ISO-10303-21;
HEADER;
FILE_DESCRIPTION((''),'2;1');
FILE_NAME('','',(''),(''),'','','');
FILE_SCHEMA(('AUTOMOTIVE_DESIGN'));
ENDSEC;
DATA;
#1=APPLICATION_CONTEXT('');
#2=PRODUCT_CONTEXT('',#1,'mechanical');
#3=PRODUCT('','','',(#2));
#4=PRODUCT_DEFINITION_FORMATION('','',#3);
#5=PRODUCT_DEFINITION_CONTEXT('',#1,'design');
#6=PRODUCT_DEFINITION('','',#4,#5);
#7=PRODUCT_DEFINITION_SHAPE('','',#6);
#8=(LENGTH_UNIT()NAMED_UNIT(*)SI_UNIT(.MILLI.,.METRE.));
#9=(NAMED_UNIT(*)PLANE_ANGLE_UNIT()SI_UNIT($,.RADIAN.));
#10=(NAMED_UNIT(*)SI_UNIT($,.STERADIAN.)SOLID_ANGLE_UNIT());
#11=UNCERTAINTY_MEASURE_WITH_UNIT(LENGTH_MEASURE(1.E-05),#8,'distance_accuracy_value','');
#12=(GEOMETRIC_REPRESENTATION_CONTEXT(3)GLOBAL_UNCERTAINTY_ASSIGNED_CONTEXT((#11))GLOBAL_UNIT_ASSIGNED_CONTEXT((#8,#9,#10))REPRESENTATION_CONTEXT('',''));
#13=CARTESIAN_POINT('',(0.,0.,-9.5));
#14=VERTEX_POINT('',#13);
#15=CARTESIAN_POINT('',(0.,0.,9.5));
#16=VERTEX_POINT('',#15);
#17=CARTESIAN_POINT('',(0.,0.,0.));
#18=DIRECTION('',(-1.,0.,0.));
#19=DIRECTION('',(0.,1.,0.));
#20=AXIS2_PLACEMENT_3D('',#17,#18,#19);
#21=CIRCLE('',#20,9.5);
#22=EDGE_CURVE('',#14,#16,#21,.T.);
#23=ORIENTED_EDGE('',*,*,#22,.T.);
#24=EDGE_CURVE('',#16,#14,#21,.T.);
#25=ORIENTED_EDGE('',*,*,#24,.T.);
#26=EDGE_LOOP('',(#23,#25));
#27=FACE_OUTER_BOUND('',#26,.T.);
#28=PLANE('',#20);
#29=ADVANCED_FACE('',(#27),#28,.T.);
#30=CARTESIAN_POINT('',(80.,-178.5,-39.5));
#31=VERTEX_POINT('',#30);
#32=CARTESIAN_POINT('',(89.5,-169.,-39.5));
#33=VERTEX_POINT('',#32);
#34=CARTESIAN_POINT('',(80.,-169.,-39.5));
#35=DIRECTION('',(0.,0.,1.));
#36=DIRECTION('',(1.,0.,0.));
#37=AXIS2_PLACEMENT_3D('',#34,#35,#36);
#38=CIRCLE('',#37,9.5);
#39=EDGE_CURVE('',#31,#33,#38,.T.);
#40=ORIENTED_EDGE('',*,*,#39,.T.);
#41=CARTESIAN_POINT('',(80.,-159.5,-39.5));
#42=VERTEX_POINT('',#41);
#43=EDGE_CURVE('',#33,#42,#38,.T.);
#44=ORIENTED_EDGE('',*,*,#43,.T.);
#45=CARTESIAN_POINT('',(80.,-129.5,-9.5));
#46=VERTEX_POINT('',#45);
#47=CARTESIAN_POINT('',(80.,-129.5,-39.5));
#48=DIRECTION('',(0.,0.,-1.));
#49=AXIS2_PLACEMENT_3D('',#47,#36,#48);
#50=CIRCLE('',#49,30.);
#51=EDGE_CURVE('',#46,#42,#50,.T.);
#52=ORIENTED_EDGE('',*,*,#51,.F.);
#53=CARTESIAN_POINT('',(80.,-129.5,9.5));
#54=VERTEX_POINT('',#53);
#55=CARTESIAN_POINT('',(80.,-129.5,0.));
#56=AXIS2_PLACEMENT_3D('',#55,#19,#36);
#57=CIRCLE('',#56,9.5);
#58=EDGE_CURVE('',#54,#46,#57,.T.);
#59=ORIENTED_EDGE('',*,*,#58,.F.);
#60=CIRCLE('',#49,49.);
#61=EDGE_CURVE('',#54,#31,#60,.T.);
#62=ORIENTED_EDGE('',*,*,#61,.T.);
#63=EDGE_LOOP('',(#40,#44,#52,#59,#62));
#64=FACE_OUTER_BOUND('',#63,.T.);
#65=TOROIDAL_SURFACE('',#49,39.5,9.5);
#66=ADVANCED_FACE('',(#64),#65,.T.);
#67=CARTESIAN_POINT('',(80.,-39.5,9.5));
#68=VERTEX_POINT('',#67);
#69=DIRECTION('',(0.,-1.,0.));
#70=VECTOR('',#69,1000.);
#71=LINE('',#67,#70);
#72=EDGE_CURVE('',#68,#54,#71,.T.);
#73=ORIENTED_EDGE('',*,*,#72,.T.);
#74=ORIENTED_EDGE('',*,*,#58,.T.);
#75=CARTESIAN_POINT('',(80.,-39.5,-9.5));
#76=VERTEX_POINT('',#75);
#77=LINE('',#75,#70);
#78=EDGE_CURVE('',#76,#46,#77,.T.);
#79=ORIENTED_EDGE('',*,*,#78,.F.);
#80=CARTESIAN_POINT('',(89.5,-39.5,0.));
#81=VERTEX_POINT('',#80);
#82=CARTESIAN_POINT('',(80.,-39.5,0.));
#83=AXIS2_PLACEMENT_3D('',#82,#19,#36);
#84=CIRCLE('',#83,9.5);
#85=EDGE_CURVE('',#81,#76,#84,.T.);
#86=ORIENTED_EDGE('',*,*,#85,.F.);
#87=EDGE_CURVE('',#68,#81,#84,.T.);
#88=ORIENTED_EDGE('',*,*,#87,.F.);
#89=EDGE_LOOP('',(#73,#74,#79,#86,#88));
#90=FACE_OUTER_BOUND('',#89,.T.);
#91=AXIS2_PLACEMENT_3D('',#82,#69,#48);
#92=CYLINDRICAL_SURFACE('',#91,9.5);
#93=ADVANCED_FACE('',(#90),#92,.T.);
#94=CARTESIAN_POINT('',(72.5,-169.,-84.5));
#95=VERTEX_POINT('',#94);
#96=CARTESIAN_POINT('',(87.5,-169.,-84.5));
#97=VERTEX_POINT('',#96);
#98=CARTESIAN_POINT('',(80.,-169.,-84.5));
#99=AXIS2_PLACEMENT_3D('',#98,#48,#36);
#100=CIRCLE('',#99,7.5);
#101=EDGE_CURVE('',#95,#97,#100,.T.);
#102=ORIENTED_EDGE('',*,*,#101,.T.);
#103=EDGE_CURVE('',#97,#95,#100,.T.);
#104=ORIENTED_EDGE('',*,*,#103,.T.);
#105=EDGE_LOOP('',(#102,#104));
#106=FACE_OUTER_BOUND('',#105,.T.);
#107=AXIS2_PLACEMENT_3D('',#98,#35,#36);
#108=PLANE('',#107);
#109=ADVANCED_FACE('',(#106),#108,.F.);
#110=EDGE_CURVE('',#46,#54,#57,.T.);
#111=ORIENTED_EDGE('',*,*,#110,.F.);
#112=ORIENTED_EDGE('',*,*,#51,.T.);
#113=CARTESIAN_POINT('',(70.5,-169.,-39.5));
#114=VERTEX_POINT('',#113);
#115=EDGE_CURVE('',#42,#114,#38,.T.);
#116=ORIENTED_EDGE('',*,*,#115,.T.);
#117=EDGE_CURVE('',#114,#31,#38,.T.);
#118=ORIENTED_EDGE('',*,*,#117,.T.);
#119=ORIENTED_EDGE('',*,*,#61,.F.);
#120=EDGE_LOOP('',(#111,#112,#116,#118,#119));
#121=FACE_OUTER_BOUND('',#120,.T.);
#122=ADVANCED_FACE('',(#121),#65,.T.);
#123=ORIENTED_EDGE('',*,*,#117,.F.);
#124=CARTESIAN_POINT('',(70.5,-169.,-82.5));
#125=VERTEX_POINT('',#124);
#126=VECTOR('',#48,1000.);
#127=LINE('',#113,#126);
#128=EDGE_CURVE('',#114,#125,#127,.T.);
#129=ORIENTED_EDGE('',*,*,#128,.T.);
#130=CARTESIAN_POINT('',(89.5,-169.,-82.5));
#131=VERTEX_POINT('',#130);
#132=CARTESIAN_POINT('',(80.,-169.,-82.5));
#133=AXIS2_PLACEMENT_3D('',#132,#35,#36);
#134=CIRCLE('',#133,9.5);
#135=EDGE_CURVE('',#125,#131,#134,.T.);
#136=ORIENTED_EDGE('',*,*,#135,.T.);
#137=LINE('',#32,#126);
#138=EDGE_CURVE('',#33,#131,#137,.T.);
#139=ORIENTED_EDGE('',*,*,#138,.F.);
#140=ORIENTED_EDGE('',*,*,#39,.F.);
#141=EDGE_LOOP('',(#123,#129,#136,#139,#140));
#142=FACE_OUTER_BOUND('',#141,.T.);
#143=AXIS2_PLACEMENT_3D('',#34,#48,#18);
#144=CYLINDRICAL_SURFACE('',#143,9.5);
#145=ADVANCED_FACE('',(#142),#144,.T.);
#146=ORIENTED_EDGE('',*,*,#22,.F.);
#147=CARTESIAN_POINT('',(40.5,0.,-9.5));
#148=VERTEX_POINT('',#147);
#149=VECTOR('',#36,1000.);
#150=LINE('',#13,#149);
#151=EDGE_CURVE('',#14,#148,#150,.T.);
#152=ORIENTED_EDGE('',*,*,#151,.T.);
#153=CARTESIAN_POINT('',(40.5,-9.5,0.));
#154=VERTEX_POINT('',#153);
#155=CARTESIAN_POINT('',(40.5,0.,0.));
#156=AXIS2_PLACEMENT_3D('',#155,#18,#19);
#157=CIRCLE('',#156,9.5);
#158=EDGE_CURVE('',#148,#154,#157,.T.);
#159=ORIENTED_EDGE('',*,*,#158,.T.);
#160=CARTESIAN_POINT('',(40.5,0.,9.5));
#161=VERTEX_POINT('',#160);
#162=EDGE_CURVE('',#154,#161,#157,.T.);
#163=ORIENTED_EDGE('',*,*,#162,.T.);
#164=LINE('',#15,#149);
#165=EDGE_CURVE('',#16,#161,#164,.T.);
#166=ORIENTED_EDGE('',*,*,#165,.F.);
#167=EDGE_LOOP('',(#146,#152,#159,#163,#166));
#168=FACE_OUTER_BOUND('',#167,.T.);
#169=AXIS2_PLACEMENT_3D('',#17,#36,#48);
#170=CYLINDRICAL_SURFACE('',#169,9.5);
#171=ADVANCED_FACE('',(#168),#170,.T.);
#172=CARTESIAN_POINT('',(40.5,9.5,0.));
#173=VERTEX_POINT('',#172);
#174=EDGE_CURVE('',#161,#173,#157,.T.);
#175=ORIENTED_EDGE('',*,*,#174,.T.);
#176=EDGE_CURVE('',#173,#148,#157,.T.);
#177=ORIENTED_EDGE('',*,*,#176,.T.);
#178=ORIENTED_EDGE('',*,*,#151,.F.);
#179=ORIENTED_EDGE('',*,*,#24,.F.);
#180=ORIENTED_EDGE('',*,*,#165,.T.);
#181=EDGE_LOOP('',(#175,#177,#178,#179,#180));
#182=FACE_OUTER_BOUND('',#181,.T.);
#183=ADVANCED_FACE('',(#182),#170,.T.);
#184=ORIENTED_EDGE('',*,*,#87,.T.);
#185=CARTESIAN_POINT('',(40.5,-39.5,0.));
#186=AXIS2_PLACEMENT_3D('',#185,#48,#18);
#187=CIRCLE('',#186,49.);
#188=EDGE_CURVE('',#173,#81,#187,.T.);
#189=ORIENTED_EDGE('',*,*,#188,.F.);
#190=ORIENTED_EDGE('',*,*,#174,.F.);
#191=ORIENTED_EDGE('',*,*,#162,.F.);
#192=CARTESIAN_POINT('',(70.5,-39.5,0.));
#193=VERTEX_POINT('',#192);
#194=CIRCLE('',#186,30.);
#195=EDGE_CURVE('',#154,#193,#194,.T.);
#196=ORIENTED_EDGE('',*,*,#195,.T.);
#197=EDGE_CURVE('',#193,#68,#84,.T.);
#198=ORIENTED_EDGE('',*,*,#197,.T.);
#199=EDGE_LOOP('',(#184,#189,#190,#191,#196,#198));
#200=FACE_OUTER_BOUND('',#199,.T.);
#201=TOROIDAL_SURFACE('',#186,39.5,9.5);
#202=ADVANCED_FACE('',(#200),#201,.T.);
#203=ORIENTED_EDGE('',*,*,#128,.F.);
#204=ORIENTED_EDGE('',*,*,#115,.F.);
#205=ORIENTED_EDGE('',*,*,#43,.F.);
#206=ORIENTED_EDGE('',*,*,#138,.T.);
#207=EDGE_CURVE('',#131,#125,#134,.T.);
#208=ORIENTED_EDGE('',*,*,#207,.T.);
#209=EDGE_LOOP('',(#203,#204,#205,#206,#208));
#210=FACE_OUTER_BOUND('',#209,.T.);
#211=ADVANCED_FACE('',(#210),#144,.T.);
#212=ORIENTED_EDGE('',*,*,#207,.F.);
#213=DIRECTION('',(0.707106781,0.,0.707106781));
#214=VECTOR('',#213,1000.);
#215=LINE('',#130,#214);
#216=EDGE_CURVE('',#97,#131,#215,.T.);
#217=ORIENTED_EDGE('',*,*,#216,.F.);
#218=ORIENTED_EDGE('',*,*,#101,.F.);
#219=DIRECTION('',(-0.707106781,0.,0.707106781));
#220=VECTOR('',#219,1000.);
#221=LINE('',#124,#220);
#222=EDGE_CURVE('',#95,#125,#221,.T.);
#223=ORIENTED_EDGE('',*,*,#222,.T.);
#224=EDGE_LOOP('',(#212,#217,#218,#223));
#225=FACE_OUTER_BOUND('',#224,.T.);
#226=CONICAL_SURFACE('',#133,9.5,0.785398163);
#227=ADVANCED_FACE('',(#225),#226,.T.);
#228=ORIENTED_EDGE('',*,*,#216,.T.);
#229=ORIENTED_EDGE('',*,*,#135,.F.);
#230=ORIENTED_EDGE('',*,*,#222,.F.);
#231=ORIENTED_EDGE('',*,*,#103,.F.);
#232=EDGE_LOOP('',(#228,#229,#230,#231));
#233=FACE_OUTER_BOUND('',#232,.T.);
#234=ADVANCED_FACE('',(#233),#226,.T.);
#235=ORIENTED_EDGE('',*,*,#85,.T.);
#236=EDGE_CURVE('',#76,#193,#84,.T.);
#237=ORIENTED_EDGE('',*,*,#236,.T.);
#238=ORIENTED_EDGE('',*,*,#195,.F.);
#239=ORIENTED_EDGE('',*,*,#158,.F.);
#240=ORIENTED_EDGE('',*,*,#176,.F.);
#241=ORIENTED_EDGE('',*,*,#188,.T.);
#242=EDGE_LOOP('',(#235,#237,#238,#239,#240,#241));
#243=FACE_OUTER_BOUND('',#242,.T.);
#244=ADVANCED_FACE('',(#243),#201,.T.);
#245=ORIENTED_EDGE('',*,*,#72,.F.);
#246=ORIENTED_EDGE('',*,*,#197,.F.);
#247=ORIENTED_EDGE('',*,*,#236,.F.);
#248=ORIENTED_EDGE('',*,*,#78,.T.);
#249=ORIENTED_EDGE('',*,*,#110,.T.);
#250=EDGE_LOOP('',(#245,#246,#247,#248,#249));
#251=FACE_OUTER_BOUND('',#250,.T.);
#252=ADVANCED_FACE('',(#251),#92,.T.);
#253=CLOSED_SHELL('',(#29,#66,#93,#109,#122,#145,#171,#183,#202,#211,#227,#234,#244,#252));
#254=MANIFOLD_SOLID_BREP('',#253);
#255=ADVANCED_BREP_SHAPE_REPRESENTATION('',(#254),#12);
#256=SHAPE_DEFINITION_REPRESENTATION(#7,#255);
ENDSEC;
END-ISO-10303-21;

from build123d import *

# Parameters (mm, degrees)
SWEEP1_PROFILE_R = 9.5
CHAMFER1_SIZE    = 2


with BuildPart() as part:
    # Sweep1: sweep along a curve in space
    with BuildLine() as sweep1_path:
        Line((0, 0, 0), (40.5, 0, 0))
        ThreePointArc((40.5, 0, 0), (68.430717857, -11.569282143, 0), (80, -39.5, 0))
        Line((80, -39.5, 0), (80, -129.5, 0))
        ThreePointArc((80, -129.5, 0), (80, -157.430717857, -11.569282143), (80, -169, -39.5))
        Line((80, -169, -39.5), (80, -169, -84.5))
    # Sweep1 profile (on start of the path) → Sweep1 (sweep)
    with BuildSketch(Plane(origin=(0, 0, 0), x_dir=(0, 0, 1), z_dir=(1, 0, 0))):
        Circle(SWEEP1_PROFILE_R)
    sweep(path=sweep1_path.line)

    # Chamfer1
    chamfer1_edges = [part.edges().sort_by_distance(p)[0] for p in [
        (80, -159.5, -84.5),
    ]]
    chamfer(chamfer1_edges, length=CHAMFER1_SIZE)


solid = part.part
